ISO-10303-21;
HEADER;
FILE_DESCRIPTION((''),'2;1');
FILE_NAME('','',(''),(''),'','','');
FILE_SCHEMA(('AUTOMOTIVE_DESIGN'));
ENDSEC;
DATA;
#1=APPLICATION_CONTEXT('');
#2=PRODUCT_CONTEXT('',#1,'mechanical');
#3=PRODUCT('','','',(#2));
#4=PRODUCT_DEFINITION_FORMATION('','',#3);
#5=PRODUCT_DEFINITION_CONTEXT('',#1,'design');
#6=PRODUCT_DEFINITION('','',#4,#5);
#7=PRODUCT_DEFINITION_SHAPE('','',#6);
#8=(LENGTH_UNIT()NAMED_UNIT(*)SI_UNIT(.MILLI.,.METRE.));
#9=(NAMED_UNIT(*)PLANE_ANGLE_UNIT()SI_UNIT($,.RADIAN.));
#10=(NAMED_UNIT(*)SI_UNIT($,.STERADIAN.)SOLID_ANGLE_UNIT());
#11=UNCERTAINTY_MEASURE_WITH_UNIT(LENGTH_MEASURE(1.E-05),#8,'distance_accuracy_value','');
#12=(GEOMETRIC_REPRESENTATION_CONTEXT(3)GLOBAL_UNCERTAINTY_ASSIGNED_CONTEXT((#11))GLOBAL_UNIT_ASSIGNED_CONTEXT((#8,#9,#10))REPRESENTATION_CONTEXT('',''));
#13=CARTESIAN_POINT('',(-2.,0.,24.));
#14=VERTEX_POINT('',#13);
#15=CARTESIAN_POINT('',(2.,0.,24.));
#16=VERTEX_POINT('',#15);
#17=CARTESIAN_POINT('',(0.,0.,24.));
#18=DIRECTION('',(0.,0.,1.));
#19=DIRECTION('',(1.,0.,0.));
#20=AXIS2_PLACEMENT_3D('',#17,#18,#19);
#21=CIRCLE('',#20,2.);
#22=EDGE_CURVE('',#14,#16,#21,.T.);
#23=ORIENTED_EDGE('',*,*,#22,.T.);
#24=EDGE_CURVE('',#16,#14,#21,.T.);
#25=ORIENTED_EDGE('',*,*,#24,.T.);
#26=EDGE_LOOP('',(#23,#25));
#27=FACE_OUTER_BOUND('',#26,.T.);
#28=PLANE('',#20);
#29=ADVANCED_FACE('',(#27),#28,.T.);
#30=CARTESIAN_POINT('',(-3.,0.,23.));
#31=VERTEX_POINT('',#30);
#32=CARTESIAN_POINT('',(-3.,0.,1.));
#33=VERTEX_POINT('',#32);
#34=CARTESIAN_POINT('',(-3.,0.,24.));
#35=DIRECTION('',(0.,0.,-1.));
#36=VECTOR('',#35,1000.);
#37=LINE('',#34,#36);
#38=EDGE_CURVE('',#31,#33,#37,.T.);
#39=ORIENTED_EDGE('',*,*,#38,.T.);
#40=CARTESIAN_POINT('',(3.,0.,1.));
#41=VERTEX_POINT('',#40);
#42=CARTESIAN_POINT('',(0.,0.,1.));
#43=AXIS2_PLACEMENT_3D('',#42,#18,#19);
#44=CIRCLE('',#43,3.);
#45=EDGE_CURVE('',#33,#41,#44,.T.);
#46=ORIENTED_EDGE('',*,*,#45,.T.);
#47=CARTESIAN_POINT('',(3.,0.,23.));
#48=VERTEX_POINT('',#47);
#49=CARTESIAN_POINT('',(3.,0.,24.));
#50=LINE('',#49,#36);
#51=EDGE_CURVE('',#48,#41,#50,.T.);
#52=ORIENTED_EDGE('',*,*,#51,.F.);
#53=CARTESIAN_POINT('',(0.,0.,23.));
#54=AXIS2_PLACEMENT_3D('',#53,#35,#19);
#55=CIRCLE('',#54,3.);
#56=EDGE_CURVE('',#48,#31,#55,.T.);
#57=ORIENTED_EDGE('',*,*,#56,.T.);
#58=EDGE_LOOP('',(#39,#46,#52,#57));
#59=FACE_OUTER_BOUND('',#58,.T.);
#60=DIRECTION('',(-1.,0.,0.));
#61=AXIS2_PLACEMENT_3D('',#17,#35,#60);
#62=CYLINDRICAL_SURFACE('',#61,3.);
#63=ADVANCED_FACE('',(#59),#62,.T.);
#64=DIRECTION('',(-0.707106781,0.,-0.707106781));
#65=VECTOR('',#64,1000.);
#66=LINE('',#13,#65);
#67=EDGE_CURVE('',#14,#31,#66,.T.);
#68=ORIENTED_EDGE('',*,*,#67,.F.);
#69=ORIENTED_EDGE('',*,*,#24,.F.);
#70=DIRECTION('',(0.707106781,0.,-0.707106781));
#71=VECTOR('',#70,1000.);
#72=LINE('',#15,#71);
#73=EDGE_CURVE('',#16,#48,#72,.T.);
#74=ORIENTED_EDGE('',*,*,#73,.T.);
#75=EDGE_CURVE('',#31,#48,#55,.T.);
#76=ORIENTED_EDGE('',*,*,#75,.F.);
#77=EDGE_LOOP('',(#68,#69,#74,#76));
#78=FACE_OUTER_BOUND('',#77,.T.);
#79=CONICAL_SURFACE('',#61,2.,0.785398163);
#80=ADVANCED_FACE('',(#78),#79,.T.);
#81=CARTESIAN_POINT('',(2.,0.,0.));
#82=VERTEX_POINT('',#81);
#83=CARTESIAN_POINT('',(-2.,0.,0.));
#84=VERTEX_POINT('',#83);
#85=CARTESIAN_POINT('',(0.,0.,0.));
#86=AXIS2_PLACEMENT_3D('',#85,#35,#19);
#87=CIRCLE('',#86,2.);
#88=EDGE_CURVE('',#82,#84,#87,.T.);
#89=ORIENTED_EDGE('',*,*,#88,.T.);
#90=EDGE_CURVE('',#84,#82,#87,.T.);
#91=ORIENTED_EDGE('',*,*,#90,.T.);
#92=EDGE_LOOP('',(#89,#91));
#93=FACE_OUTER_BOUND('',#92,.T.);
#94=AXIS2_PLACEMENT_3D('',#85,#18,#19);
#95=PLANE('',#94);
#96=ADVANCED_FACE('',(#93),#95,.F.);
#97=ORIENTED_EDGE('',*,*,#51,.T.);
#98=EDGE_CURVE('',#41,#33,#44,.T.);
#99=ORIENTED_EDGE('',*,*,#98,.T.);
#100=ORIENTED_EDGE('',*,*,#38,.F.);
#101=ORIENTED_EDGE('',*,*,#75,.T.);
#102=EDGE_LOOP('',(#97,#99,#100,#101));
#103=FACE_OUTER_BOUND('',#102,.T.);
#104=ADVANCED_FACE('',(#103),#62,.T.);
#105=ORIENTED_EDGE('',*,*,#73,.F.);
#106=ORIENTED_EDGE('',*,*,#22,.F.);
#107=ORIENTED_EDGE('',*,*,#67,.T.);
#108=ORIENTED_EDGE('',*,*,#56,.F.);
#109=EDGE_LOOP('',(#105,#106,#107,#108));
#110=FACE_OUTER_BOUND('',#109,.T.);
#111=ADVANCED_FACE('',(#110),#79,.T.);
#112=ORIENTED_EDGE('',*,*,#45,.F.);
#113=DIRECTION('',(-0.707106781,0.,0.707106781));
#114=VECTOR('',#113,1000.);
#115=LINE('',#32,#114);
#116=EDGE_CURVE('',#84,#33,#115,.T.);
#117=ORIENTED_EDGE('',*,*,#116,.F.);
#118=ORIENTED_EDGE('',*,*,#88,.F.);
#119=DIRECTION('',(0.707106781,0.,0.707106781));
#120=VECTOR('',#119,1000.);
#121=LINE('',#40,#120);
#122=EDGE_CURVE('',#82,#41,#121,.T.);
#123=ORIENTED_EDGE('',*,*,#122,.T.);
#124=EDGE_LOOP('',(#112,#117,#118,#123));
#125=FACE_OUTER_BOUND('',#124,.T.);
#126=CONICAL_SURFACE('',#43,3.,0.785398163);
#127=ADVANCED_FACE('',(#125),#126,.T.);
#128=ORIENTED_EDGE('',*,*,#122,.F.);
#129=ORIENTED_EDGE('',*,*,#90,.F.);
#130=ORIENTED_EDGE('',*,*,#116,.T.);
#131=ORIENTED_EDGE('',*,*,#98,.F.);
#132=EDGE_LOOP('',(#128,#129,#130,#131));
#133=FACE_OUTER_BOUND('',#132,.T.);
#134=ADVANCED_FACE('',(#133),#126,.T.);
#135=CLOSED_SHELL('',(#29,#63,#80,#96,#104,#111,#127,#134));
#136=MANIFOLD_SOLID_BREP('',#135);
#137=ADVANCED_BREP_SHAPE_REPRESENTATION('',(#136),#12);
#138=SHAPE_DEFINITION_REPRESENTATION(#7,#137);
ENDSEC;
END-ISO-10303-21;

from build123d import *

# Parameters (mm, degrees)
SKETCH1_R           = 3
BOSS_EXTRUDE1_DEPTH = 24
CHAMFER1_SIZE       = 1


with BuildPart() as part:
    # Sketch1 → Boss-Extrude1 (new body)
    with BuildSketch(Plane.XY):
        Circle(SKETCH1_R)
    extrude(amount=BOSS_EXTRUDE1_DEPTH)

    # Chamfer1
    chamfer1_edges = [part.edges().sort_by_distance(p)[0] for p in [
        (-3, 0, 0),
        (-3, 0, 24),
    ]]
    chamfer(chamfer1_edges, length=CHAMFER1_SIZE)


solid = part.part
